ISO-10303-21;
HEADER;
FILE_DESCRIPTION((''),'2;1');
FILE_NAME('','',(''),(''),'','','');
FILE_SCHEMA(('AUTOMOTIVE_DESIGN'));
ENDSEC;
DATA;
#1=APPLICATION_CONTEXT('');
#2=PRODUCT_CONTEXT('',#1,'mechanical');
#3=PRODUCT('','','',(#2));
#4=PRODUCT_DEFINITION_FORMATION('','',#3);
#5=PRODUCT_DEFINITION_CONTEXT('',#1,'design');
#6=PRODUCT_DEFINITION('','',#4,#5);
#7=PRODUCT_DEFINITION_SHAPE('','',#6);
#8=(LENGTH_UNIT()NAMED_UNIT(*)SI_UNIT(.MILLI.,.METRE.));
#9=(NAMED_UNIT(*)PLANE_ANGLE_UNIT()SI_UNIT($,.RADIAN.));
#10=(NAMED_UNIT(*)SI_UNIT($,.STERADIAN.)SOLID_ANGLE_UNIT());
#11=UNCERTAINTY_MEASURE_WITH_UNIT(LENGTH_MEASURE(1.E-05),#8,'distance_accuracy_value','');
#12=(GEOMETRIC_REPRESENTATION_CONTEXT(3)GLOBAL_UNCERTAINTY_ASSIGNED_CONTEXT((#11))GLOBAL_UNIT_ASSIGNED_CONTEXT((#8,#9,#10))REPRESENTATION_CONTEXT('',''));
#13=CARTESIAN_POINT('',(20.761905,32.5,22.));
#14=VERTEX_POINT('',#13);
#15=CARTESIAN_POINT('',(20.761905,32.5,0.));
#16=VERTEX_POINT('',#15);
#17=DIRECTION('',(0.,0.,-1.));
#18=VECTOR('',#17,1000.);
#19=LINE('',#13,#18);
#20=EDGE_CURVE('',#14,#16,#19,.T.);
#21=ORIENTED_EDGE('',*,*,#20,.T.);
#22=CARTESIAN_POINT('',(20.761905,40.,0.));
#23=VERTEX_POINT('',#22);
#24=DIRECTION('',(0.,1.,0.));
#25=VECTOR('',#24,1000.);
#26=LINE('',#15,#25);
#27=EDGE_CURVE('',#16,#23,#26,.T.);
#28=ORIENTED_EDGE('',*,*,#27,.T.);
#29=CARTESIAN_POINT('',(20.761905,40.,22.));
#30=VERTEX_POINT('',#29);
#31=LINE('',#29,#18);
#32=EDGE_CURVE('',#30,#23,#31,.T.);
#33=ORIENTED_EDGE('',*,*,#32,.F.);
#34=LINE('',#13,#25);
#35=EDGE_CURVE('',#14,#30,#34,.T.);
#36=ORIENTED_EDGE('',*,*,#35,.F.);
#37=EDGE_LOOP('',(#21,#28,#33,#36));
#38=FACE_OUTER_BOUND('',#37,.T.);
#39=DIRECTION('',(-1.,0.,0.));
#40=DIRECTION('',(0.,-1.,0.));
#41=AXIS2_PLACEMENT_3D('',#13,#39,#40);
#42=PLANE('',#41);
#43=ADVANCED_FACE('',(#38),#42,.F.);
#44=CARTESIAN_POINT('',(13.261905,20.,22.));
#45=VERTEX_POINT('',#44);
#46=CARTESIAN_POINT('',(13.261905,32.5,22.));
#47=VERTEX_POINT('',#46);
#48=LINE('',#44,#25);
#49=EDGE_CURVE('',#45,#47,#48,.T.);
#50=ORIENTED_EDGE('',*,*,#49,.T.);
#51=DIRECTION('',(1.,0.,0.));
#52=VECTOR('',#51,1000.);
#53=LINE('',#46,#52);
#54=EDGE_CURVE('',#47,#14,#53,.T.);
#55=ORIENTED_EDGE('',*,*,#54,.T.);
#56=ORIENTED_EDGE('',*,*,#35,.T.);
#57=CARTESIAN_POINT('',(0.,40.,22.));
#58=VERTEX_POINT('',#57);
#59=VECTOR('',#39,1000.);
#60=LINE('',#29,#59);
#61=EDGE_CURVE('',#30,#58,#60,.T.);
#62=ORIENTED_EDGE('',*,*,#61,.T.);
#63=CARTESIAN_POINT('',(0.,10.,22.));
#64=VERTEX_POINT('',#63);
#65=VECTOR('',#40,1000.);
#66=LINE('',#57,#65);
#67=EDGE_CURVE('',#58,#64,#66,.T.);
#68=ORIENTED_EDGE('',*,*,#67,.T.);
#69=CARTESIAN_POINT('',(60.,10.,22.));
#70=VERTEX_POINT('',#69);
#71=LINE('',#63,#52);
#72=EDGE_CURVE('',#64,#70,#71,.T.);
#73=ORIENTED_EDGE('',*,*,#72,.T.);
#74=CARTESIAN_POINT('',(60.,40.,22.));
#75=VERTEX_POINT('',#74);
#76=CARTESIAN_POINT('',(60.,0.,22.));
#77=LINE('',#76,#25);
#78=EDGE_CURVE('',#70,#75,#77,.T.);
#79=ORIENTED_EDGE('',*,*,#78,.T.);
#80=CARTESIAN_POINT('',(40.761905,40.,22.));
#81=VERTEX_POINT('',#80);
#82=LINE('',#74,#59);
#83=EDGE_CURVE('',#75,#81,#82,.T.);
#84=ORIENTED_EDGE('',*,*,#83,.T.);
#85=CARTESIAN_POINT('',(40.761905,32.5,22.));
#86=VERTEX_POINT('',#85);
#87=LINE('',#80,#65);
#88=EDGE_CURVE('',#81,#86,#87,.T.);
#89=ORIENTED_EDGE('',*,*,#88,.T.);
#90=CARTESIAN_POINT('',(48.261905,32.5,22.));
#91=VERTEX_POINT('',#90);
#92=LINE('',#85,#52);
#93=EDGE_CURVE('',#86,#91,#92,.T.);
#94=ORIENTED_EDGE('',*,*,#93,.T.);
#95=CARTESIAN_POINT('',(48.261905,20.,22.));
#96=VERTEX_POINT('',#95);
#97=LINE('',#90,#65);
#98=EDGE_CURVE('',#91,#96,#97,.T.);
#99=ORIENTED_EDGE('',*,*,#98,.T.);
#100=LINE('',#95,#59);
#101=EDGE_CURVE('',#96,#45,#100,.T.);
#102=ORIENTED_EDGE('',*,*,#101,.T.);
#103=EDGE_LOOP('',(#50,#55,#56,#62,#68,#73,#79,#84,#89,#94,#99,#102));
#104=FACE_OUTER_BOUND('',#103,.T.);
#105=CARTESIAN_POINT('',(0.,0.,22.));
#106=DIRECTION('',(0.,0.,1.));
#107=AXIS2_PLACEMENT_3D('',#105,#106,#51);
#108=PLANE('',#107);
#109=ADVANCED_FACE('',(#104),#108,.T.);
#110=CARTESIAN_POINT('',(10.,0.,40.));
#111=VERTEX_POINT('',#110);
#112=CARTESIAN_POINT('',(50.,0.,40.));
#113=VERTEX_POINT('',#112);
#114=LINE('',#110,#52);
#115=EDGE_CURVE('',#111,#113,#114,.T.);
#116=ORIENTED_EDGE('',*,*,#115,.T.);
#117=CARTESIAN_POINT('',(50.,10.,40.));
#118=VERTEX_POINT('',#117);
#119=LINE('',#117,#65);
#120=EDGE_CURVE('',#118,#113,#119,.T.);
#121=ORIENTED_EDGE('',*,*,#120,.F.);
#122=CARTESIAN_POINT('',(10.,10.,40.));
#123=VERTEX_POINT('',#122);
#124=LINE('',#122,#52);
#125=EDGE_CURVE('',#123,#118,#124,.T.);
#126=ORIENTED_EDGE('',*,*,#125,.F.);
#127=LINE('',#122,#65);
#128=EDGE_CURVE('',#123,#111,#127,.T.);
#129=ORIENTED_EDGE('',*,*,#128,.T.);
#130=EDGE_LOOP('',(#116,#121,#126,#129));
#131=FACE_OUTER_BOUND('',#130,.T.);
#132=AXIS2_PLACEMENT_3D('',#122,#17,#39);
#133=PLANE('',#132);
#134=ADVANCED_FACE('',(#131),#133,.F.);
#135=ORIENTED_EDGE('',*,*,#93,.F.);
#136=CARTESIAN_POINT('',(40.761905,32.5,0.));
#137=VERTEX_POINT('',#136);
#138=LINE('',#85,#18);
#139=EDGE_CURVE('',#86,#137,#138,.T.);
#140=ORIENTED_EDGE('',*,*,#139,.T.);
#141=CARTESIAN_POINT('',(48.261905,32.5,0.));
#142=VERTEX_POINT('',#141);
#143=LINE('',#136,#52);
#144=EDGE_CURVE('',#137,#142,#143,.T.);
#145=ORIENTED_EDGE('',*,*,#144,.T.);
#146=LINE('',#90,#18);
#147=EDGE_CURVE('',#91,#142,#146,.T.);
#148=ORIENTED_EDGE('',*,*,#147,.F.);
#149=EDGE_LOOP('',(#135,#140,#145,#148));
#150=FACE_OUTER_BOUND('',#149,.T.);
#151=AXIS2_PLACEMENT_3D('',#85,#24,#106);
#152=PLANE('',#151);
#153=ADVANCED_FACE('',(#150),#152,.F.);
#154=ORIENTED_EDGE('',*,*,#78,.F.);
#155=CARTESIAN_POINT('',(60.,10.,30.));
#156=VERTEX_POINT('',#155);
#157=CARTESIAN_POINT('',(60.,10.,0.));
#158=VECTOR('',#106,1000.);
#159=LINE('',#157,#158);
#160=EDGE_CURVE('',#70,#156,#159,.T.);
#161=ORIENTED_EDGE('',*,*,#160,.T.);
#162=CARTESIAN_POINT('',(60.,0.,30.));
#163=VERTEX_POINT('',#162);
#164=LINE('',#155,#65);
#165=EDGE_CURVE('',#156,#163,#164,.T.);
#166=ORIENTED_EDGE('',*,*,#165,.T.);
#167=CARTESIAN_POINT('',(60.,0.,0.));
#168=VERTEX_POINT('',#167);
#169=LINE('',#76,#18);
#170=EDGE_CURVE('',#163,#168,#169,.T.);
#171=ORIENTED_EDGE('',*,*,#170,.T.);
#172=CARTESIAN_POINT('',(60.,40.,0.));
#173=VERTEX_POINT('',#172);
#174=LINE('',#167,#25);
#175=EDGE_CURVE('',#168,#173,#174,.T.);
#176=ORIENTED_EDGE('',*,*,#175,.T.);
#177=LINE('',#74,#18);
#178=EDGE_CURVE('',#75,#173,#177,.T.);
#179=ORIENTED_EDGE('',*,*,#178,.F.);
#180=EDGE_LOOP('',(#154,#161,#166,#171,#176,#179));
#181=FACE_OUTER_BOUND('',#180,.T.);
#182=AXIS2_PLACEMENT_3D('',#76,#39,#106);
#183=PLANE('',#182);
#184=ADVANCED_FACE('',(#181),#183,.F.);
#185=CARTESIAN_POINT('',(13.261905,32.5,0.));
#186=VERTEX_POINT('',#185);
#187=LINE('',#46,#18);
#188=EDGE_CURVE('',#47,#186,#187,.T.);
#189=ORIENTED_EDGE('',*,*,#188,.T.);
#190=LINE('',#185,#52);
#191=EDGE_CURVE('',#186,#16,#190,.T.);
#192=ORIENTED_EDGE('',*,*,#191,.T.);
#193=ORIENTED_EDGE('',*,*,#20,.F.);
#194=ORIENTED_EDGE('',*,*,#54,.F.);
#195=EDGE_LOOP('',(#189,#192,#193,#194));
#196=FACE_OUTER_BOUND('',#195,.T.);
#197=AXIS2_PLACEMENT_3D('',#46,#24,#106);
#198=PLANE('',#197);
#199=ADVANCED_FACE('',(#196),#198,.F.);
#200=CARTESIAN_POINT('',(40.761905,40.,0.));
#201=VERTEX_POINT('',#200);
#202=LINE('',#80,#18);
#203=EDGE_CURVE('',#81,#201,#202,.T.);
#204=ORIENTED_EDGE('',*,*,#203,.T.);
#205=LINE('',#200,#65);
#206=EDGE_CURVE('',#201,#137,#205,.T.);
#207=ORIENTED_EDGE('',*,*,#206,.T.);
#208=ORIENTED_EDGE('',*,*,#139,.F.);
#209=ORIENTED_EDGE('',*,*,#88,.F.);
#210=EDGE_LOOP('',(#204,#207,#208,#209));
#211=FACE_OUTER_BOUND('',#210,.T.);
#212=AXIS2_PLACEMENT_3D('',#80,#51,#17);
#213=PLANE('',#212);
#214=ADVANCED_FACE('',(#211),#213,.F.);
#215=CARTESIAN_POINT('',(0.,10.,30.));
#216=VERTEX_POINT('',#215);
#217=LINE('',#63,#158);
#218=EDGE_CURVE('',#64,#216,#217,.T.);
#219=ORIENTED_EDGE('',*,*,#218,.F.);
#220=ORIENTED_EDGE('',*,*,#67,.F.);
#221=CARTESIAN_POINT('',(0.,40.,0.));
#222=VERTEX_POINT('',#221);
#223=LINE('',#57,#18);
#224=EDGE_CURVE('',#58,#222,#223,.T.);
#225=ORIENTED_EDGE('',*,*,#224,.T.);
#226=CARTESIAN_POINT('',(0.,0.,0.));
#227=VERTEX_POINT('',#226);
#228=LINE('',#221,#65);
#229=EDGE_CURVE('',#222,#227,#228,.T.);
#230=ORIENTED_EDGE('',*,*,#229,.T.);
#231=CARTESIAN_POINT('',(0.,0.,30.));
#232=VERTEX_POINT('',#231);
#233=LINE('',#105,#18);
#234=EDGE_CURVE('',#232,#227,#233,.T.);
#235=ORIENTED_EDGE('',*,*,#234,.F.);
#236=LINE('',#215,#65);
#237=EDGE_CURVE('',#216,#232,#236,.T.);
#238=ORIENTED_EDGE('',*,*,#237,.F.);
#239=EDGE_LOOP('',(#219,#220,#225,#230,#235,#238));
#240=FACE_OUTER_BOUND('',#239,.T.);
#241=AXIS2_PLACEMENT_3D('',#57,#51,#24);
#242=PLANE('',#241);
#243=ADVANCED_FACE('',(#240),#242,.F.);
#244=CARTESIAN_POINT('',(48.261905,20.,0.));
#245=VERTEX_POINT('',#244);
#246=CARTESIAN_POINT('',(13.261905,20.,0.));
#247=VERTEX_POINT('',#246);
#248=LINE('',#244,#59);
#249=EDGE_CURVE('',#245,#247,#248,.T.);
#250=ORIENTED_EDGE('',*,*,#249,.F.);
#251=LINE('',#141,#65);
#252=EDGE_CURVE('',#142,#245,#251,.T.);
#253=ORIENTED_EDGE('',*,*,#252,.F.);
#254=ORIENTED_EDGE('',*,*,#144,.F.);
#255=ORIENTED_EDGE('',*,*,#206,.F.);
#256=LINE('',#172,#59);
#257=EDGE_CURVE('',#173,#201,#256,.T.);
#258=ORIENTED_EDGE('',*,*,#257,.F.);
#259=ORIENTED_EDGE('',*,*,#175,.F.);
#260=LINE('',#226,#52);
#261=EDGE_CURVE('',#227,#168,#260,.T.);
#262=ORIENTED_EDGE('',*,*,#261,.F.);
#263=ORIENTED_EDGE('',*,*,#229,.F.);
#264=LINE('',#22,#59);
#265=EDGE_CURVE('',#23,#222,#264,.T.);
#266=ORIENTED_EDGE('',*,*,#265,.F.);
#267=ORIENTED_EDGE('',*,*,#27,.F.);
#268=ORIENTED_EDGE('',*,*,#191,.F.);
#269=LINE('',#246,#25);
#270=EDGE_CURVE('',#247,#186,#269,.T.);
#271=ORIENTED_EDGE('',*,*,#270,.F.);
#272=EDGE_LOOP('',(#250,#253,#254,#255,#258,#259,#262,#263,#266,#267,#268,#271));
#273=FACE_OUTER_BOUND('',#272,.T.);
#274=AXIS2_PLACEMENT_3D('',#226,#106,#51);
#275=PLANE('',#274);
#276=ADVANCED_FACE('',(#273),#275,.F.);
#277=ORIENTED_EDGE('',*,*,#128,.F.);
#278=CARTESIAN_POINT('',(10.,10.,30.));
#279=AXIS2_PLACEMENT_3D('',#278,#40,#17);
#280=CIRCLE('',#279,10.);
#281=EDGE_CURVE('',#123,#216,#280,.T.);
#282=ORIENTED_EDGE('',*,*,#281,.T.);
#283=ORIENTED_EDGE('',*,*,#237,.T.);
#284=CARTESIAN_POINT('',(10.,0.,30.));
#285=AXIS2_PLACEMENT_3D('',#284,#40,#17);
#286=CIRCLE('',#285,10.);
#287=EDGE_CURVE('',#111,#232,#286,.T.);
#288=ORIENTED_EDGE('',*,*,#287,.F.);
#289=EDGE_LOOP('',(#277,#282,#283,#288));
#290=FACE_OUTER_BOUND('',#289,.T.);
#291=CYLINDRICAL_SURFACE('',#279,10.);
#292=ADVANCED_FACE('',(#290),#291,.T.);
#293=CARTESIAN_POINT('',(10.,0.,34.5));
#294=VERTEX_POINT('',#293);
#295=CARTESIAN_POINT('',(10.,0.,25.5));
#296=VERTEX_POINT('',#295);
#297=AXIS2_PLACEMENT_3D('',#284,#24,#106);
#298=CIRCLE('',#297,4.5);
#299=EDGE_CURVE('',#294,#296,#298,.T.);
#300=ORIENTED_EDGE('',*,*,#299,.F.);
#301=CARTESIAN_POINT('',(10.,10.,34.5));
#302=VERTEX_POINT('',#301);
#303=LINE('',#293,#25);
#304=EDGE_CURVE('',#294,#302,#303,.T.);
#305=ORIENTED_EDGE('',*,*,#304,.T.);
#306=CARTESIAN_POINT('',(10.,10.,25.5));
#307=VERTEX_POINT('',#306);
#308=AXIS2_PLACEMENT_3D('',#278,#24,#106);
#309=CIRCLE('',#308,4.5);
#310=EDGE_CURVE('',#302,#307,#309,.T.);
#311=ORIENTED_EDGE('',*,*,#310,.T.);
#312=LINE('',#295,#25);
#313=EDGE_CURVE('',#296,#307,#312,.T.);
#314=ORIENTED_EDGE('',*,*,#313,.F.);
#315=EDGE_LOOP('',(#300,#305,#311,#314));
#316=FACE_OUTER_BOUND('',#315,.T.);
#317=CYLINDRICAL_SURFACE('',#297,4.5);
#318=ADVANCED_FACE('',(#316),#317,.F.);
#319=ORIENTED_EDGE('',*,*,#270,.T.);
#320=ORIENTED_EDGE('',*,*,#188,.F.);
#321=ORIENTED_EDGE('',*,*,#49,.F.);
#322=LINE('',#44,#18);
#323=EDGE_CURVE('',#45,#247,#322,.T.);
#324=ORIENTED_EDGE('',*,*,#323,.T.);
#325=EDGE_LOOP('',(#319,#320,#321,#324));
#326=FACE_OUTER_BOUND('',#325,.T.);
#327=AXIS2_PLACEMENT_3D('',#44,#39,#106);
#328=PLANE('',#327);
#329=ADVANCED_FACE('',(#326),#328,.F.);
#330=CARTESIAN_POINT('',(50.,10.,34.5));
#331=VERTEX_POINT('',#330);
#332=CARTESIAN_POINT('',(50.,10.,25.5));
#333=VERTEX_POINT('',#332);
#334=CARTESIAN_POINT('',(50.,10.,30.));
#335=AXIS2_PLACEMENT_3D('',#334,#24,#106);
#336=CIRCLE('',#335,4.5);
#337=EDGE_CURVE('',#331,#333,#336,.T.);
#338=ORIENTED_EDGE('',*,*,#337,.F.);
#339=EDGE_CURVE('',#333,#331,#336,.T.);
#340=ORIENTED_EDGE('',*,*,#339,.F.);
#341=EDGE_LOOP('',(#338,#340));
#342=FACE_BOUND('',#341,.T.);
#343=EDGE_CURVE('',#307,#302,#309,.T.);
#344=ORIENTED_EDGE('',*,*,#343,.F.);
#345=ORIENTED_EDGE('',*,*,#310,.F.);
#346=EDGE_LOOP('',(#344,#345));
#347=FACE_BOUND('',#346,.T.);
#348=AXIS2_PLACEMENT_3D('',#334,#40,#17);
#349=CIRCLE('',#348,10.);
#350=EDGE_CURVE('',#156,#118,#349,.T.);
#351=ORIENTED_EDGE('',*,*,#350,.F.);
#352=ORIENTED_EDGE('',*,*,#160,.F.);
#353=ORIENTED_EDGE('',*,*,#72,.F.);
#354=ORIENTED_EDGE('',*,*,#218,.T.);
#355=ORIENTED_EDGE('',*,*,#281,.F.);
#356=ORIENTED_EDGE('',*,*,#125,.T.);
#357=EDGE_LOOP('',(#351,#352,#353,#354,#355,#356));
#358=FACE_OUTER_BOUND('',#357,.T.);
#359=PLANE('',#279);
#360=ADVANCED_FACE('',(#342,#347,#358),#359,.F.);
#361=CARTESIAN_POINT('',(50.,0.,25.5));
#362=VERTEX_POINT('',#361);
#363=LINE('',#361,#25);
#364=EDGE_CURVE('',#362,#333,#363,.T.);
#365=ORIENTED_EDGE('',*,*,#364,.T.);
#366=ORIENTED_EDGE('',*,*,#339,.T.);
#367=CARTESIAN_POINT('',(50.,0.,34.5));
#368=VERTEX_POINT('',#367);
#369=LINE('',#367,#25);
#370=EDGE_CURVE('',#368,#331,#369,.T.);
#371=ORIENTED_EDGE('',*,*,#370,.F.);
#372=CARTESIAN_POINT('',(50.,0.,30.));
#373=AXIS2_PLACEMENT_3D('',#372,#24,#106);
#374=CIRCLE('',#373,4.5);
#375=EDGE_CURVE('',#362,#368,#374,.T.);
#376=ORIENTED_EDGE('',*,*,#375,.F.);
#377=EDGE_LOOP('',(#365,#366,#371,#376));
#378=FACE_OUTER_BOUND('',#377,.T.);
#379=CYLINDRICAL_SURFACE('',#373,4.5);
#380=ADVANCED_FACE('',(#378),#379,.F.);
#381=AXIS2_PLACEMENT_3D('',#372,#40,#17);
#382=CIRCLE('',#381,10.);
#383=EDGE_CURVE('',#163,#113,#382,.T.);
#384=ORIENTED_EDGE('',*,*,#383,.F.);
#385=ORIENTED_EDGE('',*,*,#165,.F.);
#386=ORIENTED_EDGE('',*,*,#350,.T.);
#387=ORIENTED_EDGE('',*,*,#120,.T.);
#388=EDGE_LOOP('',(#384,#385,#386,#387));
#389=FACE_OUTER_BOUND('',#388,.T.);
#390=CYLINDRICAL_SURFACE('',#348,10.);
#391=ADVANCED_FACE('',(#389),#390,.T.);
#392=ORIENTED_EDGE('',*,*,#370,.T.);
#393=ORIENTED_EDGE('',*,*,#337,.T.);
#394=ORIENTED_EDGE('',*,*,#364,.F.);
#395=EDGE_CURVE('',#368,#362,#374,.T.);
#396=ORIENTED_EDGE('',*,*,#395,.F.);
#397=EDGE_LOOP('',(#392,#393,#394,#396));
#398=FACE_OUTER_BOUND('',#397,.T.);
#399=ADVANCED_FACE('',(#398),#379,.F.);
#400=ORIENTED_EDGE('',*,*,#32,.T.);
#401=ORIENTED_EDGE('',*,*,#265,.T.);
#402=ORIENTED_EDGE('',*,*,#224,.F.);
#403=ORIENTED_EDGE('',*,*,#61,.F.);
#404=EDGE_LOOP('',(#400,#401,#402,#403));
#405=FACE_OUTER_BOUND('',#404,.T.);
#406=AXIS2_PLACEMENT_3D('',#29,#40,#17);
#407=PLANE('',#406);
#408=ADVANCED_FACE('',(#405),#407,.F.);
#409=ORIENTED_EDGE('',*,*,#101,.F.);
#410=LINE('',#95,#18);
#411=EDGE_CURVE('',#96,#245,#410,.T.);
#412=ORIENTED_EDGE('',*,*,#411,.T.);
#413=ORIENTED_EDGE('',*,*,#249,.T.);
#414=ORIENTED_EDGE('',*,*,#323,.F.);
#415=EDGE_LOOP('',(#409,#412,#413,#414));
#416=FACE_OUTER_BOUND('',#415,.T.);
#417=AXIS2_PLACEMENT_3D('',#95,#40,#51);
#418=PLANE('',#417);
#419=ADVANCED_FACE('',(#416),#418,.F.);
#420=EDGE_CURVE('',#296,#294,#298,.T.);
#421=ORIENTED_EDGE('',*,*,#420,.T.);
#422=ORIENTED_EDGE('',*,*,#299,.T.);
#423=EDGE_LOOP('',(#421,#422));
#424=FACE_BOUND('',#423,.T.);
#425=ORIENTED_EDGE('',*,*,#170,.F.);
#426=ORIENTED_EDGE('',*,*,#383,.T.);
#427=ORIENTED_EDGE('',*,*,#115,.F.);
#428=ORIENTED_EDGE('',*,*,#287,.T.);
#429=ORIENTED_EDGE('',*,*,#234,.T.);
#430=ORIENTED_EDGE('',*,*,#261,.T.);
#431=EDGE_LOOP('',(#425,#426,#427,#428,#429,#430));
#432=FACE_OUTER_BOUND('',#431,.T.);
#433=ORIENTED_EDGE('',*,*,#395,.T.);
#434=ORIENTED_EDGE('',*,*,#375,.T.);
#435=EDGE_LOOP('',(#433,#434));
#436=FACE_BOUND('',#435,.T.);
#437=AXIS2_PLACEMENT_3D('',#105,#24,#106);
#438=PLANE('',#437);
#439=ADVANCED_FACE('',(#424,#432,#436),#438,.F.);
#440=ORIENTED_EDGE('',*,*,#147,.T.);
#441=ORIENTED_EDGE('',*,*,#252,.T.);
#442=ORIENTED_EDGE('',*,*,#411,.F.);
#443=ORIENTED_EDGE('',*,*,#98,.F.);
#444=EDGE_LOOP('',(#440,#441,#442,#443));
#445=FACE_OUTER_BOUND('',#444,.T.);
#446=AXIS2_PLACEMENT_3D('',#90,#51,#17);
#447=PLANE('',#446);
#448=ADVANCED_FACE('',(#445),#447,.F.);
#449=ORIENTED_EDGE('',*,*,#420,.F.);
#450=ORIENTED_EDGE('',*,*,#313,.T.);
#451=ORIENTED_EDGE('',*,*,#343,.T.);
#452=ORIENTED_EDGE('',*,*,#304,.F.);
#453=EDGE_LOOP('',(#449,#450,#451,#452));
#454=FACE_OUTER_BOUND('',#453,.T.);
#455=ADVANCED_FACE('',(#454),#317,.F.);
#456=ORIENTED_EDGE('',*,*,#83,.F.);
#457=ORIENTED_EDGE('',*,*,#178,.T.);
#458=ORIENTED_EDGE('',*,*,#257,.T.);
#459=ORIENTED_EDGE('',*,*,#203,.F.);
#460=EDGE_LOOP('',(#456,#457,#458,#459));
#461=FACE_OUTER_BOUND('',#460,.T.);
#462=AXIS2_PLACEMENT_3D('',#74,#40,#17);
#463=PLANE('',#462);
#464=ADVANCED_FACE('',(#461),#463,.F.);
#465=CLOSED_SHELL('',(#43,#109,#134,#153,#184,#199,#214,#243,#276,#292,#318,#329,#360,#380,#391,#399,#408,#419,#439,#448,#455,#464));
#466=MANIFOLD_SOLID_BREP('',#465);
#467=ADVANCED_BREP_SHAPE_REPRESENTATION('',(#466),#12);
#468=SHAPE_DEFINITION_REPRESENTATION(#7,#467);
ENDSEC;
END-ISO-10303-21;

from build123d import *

# Parameters (mm, degrees)
U_BRACKET_BODY_DEPTH      = 22
BASE_PLATE_DEPTH          = 10
MOUNTING_HOLES_SKETCH_R   = 4.5
MOUNTING_HOLES_2X_9_DEPTH = 79.102496759


with BuildPart() as part:
    # U-Bracket Profile Sketch → U-Bracket Body (new body)
    with BuildSketch(Plane.XY):
        Polygon((0, 0), (60, 0), (60, 40), (40.761904762, 40), (40.761904762, 32.5), (48.261904762, 32.5), (48.261904762, 20), (13.261904762, 20), (13.261904762, 32.5), (20.761904762, 32.5), (20.761904762, 40), (0, 40), align=None)
    extrude(amount=U_BRACKET_BODY_DEPTH)

    # Base Plate Sketch → Base Plate (add)
    with BuildSketch(Plane.XZ):
        with BuildLine():
            Line((0, 22), (0, 30))
            ThreePointArc((0, 30), (2.928932188, 37.071067812), (10, 40))
            Line((10, 40), (50, 40))
            ThreePointArc((50, 40), (57.071067812, 37.071067812), (60, 30))
            Line((60, 30), (60, 22))
            Line((60, 22), (60, 0))
            Line((60, 0), (0, 0))
            Line((0, 0), (0, 22))
        make_face()
    extrude(amount=-BASE_PLATE_DEPTH)

    # Mounting Holes Sketch → Mounting Holes 2xØ9 (cut, through all)
    with BuildSketch(Plane(origin=(0, 10, 0), x_dir=(1, 0, 0), z_dir=(0, 1, 0))):
        with Locations(Location((10, -30, 0), (0, 0, 270))):
            Circle(MOUNTING_HOLES_SKETCH_R)
        with Locations(Location((50, -30, 0), (0, 0, 270))):
            Circle(MOUNTING_HOLES_SKETCH_R)
    extrude(amount=-MOUNTING_HOLES_2X_9_DEPTH, mode=Mode.SUBTRACT)


solid = part.part
